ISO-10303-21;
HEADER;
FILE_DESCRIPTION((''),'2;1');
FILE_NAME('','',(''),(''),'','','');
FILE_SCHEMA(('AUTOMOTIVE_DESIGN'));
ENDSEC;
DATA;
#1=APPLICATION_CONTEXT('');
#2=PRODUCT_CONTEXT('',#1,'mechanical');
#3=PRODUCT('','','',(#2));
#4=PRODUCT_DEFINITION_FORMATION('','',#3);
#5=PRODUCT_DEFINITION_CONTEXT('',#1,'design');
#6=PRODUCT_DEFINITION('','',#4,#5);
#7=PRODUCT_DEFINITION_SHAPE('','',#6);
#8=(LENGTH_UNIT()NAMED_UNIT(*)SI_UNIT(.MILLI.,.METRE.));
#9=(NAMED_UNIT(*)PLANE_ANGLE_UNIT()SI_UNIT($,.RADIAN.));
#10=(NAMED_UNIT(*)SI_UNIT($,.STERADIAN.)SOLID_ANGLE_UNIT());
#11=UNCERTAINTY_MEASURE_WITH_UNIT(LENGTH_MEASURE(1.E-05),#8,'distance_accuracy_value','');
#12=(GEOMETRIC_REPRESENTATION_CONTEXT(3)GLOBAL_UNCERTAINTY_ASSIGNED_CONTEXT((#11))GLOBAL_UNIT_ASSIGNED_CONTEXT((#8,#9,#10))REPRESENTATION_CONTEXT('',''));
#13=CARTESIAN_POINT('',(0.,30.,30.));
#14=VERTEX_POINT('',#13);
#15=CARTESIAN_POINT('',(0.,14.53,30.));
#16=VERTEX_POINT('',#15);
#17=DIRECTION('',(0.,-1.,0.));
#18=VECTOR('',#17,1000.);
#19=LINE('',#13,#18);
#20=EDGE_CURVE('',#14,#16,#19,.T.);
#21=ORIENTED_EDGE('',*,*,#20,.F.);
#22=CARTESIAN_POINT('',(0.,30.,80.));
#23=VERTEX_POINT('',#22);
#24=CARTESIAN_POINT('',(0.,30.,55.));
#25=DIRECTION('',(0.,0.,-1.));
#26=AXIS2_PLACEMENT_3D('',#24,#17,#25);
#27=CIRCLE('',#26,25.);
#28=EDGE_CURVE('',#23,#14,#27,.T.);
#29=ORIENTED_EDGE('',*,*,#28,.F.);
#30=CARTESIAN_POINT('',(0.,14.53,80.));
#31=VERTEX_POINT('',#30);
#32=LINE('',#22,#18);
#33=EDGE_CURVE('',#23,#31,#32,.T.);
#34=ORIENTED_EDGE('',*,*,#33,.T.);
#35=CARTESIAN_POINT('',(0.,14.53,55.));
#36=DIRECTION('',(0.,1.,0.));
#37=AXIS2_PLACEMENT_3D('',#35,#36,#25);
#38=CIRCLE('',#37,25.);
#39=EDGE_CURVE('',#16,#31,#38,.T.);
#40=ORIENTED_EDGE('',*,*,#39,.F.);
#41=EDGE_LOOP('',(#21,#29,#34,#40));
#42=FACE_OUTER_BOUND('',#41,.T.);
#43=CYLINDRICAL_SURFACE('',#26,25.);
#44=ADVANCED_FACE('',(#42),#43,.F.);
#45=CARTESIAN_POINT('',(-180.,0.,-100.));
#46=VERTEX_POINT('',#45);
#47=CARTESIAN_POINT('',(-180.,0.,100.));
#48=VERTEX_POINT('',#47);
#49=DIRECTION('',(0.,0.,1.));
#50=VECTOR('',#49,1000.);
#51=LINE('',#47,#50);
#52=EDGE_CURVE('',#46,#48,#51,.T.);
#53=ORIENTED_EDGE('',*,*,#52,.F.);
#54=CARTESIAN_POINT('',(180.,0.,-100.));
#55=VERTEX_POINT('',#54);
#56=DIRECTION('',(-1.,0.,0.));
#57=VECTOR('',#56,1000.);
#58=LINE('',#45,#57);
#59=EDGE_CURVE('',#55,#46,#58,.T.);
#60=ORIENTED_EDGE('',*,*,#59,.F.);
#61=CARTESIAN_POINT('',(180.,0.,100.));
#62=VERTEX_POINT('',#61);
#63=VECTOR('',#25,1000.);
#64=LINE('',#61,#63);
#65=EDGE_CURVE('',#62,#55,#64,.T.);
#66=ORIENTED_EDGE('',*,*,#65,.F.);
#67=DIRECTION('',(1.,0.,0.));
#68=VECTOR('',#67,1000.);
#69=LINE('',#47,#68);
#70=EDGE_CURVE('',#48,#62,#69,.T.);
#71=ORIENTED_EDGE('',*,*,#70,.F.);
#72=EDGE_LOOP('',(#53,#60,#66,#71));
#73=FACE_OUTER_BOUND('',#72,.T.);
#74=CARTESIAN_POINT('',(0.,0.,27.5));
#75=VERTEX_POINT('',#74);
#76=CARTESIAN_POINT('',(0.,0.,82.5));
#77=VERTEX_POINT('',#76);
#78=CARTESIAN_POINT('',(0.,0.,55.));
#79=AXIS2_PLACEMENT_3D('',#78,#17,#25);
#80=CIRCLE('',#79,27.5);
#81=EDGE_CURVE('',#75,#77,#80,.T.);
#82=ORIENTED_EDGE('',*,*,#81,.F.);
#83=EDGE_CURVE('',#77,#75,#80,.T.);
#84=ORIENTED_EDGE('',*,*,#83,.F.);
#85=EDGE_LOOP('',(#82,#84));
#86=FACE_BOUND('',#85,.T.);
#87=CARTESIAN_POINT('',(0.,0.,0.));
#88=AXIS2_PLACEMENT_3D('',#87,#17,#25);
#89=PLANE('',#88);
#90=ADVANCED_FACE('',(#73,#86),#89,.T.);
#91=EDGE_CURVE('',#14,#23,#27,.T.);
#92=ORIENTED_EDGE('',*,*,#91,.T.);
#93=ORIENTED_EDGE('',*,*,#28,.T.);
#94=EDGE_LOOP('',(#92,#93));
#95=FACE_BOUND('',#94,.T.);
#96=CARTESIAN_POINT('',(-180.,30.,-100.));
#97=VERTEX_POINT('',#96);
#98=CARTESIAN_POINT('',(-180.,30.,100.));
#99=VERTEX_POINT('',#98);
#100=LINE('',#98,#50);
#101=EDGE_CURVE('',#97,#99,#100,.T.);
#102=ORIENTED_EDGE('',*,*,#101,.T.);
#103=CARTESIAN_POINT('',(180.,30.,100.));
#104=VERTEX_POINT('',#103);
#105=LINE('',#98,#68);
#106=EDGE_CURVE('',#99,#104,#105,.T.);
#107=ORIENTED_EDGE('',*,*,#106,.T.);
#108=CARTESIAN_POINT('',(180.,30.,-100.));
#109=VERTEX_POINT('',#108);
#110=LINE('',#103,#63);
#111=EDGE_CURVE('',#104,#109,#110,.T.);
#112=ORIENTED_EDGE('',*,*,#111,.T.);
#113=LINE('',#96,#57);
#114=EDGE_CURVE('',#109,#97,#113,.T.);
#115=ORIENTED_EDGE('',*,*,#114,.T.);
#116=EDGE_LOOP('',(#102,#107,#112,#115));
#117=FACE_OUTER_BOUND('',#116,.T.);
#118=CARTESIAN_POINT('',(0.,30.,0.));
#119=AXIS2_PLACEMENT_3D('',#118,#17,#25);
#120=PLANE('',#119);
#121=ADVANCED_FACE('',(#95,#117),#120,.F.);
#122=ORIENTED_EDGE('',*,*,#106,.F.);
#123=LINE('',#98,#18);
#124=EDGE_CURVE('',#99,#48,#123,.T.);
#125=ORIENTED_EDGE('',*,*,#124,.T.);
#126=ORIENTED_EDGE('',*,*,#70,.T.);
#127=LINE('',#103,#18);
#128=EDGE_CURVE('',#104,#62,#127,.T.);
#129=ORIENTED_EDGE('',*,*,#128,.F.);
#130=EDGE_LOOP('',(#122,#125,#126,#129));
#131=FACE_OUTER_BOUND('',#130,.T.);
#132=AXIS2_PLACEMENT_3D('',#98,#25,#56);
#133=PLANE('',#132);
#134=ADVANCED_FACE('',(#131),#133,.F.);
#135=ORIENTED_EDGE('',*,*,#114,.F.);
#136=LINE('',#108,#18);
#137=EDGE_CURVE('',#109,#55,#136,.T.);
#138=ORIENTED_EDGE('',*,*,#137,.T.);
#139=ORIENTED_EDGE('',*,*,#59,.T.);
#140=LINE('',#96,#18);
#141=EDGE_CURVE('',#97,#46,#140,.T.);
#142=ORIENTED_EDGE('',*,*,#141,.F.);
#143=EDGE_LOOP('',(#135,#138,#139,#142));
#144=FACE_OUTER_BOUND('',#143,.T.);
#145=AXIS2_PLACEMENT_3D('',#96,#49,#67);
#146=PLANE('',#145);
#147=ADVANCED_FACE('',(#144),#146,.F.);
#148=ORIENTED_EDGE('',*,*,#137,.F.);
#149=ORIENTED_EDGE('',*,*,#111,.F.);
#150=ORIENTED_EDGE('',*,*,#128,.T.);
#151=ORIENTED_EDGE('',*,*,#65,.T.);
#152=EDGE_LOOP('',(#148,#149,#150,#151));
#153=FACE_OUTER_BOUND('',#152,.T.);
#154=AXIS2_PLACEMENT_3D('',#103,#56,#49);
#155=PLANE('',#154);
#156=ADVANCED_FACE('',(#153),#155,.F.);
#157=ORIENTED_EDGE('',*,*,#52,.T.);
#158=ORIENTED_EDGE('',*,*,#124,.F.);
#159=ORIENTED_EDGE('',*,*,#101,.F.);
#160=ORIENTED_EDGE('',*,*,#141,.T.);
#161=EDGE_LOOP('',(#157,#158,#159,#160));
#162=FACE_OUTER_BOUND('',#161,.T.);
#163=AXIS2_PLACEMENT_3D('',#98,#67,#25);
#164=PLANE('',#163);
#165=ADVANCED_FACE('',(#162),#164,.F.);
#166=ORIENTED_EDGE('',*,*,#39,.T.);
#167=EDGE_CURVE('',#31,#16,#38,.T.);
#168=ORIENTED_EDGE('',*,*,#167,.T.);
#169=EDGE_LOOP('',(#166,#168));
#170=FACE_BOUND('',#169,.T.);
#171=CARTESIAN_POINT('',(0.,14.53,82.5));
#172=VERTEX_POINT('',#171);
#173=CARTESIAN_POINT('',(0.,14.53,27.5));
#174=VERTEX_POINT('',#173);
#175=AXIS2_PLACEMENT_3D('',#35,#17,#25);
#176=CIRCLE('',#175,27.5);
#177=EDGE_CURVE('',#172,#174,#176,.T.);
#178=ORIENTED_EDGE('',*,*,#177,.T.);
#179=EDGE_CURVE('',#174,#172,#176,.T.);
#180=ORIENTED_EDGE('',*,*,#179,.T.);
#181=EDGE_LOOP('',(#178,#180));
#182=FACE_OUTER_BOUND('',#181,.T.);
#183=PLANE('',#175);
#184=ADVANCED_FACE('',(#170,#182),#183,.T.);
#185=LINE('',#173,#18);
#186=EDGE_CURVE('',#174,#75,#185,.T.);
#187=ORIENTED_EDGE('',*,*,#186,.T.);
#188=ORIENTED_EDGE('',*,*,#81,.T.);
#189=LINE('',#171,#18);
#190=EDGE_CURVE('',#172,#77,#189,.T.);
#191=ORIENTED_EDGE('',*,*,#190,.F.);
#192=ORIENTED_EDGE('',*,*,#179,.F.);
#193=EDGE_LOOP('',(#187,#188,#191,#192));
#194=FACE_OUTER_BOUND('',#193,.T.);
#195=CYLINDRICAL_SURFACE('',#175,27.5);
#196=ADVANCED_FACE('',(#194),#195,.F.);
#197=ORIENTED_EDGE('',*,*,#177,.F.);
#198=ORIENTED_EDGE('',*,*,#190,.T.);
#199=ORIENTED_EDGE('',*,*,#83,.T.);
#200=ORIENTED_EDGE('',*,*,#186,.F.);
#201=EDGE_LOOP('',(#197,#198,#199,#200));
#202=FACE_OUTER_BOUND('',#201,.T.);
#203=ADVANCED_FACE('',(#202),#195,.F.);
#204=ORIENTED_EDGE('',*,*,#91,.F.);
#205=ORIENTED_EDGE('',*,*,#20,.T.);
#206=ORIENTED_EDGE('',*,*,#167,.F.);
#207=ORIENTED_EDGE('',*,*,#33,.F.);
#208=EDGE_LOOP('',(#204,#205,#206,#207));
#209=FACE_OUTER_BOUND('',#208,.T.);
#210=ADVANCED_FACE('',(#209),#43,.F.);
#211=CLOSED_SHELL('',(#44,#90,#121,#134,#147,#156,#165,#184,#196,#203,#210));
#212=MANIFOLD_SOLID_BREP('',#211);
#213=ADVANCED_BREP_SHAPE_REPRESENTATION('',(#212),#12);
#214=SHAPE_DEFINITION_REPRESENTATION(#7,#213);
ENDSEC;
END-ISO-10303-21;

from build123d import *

# Parameters (mm, degrees)
SKETCH_1_W          = 360
SKETCH_1_H          = 200
EXTRUDE_1_DEPTH     = 30
SKETCH_2_R          = 25
CUT_EXTRUDE_1_DEPTH = 209.086520467
SKETCH_3_R          = 27.5
CUT_EXTRUDE_2_DEPTH = 14.53


with BuildPart() as part:
    # 草图1 → 凸台-拉伸1 (new body)
    with BuildSketch(Plane(origin=(0, 0, 0), x_dir=(1, 0, 0), z_dir=(0, 1, 0))):
        Rectangle(SKETCH_1_W, SKETCH_1_H)
    extrude(amount=EXTRUDE_1_DEPTH)

    # 草图2 → 切除-拉伸1 (cut, through all)
    with BuildSketch(Plane.XZ):
        with Locations(Location((0, 55, 0), (0, 0, 270))):
            Circle(SKETCH_2_R)
    extrude(amount=-CUT_EXTRUDE_1_DEPTH, mode=Mode.SUBTRACT)

    # 草图3 → 切除-拉伸2 (cut)
    with BuildSketch(Plane.XZ):
        with Locations(Location((0, 55, 0), (0, 0, 270))):
            Circle(SKETCH_3_R)
    extrude(amount=-CUT_EXTRUDE_2_DEPTH, mode=Mode.SUBTRACT)


solid = part.part
